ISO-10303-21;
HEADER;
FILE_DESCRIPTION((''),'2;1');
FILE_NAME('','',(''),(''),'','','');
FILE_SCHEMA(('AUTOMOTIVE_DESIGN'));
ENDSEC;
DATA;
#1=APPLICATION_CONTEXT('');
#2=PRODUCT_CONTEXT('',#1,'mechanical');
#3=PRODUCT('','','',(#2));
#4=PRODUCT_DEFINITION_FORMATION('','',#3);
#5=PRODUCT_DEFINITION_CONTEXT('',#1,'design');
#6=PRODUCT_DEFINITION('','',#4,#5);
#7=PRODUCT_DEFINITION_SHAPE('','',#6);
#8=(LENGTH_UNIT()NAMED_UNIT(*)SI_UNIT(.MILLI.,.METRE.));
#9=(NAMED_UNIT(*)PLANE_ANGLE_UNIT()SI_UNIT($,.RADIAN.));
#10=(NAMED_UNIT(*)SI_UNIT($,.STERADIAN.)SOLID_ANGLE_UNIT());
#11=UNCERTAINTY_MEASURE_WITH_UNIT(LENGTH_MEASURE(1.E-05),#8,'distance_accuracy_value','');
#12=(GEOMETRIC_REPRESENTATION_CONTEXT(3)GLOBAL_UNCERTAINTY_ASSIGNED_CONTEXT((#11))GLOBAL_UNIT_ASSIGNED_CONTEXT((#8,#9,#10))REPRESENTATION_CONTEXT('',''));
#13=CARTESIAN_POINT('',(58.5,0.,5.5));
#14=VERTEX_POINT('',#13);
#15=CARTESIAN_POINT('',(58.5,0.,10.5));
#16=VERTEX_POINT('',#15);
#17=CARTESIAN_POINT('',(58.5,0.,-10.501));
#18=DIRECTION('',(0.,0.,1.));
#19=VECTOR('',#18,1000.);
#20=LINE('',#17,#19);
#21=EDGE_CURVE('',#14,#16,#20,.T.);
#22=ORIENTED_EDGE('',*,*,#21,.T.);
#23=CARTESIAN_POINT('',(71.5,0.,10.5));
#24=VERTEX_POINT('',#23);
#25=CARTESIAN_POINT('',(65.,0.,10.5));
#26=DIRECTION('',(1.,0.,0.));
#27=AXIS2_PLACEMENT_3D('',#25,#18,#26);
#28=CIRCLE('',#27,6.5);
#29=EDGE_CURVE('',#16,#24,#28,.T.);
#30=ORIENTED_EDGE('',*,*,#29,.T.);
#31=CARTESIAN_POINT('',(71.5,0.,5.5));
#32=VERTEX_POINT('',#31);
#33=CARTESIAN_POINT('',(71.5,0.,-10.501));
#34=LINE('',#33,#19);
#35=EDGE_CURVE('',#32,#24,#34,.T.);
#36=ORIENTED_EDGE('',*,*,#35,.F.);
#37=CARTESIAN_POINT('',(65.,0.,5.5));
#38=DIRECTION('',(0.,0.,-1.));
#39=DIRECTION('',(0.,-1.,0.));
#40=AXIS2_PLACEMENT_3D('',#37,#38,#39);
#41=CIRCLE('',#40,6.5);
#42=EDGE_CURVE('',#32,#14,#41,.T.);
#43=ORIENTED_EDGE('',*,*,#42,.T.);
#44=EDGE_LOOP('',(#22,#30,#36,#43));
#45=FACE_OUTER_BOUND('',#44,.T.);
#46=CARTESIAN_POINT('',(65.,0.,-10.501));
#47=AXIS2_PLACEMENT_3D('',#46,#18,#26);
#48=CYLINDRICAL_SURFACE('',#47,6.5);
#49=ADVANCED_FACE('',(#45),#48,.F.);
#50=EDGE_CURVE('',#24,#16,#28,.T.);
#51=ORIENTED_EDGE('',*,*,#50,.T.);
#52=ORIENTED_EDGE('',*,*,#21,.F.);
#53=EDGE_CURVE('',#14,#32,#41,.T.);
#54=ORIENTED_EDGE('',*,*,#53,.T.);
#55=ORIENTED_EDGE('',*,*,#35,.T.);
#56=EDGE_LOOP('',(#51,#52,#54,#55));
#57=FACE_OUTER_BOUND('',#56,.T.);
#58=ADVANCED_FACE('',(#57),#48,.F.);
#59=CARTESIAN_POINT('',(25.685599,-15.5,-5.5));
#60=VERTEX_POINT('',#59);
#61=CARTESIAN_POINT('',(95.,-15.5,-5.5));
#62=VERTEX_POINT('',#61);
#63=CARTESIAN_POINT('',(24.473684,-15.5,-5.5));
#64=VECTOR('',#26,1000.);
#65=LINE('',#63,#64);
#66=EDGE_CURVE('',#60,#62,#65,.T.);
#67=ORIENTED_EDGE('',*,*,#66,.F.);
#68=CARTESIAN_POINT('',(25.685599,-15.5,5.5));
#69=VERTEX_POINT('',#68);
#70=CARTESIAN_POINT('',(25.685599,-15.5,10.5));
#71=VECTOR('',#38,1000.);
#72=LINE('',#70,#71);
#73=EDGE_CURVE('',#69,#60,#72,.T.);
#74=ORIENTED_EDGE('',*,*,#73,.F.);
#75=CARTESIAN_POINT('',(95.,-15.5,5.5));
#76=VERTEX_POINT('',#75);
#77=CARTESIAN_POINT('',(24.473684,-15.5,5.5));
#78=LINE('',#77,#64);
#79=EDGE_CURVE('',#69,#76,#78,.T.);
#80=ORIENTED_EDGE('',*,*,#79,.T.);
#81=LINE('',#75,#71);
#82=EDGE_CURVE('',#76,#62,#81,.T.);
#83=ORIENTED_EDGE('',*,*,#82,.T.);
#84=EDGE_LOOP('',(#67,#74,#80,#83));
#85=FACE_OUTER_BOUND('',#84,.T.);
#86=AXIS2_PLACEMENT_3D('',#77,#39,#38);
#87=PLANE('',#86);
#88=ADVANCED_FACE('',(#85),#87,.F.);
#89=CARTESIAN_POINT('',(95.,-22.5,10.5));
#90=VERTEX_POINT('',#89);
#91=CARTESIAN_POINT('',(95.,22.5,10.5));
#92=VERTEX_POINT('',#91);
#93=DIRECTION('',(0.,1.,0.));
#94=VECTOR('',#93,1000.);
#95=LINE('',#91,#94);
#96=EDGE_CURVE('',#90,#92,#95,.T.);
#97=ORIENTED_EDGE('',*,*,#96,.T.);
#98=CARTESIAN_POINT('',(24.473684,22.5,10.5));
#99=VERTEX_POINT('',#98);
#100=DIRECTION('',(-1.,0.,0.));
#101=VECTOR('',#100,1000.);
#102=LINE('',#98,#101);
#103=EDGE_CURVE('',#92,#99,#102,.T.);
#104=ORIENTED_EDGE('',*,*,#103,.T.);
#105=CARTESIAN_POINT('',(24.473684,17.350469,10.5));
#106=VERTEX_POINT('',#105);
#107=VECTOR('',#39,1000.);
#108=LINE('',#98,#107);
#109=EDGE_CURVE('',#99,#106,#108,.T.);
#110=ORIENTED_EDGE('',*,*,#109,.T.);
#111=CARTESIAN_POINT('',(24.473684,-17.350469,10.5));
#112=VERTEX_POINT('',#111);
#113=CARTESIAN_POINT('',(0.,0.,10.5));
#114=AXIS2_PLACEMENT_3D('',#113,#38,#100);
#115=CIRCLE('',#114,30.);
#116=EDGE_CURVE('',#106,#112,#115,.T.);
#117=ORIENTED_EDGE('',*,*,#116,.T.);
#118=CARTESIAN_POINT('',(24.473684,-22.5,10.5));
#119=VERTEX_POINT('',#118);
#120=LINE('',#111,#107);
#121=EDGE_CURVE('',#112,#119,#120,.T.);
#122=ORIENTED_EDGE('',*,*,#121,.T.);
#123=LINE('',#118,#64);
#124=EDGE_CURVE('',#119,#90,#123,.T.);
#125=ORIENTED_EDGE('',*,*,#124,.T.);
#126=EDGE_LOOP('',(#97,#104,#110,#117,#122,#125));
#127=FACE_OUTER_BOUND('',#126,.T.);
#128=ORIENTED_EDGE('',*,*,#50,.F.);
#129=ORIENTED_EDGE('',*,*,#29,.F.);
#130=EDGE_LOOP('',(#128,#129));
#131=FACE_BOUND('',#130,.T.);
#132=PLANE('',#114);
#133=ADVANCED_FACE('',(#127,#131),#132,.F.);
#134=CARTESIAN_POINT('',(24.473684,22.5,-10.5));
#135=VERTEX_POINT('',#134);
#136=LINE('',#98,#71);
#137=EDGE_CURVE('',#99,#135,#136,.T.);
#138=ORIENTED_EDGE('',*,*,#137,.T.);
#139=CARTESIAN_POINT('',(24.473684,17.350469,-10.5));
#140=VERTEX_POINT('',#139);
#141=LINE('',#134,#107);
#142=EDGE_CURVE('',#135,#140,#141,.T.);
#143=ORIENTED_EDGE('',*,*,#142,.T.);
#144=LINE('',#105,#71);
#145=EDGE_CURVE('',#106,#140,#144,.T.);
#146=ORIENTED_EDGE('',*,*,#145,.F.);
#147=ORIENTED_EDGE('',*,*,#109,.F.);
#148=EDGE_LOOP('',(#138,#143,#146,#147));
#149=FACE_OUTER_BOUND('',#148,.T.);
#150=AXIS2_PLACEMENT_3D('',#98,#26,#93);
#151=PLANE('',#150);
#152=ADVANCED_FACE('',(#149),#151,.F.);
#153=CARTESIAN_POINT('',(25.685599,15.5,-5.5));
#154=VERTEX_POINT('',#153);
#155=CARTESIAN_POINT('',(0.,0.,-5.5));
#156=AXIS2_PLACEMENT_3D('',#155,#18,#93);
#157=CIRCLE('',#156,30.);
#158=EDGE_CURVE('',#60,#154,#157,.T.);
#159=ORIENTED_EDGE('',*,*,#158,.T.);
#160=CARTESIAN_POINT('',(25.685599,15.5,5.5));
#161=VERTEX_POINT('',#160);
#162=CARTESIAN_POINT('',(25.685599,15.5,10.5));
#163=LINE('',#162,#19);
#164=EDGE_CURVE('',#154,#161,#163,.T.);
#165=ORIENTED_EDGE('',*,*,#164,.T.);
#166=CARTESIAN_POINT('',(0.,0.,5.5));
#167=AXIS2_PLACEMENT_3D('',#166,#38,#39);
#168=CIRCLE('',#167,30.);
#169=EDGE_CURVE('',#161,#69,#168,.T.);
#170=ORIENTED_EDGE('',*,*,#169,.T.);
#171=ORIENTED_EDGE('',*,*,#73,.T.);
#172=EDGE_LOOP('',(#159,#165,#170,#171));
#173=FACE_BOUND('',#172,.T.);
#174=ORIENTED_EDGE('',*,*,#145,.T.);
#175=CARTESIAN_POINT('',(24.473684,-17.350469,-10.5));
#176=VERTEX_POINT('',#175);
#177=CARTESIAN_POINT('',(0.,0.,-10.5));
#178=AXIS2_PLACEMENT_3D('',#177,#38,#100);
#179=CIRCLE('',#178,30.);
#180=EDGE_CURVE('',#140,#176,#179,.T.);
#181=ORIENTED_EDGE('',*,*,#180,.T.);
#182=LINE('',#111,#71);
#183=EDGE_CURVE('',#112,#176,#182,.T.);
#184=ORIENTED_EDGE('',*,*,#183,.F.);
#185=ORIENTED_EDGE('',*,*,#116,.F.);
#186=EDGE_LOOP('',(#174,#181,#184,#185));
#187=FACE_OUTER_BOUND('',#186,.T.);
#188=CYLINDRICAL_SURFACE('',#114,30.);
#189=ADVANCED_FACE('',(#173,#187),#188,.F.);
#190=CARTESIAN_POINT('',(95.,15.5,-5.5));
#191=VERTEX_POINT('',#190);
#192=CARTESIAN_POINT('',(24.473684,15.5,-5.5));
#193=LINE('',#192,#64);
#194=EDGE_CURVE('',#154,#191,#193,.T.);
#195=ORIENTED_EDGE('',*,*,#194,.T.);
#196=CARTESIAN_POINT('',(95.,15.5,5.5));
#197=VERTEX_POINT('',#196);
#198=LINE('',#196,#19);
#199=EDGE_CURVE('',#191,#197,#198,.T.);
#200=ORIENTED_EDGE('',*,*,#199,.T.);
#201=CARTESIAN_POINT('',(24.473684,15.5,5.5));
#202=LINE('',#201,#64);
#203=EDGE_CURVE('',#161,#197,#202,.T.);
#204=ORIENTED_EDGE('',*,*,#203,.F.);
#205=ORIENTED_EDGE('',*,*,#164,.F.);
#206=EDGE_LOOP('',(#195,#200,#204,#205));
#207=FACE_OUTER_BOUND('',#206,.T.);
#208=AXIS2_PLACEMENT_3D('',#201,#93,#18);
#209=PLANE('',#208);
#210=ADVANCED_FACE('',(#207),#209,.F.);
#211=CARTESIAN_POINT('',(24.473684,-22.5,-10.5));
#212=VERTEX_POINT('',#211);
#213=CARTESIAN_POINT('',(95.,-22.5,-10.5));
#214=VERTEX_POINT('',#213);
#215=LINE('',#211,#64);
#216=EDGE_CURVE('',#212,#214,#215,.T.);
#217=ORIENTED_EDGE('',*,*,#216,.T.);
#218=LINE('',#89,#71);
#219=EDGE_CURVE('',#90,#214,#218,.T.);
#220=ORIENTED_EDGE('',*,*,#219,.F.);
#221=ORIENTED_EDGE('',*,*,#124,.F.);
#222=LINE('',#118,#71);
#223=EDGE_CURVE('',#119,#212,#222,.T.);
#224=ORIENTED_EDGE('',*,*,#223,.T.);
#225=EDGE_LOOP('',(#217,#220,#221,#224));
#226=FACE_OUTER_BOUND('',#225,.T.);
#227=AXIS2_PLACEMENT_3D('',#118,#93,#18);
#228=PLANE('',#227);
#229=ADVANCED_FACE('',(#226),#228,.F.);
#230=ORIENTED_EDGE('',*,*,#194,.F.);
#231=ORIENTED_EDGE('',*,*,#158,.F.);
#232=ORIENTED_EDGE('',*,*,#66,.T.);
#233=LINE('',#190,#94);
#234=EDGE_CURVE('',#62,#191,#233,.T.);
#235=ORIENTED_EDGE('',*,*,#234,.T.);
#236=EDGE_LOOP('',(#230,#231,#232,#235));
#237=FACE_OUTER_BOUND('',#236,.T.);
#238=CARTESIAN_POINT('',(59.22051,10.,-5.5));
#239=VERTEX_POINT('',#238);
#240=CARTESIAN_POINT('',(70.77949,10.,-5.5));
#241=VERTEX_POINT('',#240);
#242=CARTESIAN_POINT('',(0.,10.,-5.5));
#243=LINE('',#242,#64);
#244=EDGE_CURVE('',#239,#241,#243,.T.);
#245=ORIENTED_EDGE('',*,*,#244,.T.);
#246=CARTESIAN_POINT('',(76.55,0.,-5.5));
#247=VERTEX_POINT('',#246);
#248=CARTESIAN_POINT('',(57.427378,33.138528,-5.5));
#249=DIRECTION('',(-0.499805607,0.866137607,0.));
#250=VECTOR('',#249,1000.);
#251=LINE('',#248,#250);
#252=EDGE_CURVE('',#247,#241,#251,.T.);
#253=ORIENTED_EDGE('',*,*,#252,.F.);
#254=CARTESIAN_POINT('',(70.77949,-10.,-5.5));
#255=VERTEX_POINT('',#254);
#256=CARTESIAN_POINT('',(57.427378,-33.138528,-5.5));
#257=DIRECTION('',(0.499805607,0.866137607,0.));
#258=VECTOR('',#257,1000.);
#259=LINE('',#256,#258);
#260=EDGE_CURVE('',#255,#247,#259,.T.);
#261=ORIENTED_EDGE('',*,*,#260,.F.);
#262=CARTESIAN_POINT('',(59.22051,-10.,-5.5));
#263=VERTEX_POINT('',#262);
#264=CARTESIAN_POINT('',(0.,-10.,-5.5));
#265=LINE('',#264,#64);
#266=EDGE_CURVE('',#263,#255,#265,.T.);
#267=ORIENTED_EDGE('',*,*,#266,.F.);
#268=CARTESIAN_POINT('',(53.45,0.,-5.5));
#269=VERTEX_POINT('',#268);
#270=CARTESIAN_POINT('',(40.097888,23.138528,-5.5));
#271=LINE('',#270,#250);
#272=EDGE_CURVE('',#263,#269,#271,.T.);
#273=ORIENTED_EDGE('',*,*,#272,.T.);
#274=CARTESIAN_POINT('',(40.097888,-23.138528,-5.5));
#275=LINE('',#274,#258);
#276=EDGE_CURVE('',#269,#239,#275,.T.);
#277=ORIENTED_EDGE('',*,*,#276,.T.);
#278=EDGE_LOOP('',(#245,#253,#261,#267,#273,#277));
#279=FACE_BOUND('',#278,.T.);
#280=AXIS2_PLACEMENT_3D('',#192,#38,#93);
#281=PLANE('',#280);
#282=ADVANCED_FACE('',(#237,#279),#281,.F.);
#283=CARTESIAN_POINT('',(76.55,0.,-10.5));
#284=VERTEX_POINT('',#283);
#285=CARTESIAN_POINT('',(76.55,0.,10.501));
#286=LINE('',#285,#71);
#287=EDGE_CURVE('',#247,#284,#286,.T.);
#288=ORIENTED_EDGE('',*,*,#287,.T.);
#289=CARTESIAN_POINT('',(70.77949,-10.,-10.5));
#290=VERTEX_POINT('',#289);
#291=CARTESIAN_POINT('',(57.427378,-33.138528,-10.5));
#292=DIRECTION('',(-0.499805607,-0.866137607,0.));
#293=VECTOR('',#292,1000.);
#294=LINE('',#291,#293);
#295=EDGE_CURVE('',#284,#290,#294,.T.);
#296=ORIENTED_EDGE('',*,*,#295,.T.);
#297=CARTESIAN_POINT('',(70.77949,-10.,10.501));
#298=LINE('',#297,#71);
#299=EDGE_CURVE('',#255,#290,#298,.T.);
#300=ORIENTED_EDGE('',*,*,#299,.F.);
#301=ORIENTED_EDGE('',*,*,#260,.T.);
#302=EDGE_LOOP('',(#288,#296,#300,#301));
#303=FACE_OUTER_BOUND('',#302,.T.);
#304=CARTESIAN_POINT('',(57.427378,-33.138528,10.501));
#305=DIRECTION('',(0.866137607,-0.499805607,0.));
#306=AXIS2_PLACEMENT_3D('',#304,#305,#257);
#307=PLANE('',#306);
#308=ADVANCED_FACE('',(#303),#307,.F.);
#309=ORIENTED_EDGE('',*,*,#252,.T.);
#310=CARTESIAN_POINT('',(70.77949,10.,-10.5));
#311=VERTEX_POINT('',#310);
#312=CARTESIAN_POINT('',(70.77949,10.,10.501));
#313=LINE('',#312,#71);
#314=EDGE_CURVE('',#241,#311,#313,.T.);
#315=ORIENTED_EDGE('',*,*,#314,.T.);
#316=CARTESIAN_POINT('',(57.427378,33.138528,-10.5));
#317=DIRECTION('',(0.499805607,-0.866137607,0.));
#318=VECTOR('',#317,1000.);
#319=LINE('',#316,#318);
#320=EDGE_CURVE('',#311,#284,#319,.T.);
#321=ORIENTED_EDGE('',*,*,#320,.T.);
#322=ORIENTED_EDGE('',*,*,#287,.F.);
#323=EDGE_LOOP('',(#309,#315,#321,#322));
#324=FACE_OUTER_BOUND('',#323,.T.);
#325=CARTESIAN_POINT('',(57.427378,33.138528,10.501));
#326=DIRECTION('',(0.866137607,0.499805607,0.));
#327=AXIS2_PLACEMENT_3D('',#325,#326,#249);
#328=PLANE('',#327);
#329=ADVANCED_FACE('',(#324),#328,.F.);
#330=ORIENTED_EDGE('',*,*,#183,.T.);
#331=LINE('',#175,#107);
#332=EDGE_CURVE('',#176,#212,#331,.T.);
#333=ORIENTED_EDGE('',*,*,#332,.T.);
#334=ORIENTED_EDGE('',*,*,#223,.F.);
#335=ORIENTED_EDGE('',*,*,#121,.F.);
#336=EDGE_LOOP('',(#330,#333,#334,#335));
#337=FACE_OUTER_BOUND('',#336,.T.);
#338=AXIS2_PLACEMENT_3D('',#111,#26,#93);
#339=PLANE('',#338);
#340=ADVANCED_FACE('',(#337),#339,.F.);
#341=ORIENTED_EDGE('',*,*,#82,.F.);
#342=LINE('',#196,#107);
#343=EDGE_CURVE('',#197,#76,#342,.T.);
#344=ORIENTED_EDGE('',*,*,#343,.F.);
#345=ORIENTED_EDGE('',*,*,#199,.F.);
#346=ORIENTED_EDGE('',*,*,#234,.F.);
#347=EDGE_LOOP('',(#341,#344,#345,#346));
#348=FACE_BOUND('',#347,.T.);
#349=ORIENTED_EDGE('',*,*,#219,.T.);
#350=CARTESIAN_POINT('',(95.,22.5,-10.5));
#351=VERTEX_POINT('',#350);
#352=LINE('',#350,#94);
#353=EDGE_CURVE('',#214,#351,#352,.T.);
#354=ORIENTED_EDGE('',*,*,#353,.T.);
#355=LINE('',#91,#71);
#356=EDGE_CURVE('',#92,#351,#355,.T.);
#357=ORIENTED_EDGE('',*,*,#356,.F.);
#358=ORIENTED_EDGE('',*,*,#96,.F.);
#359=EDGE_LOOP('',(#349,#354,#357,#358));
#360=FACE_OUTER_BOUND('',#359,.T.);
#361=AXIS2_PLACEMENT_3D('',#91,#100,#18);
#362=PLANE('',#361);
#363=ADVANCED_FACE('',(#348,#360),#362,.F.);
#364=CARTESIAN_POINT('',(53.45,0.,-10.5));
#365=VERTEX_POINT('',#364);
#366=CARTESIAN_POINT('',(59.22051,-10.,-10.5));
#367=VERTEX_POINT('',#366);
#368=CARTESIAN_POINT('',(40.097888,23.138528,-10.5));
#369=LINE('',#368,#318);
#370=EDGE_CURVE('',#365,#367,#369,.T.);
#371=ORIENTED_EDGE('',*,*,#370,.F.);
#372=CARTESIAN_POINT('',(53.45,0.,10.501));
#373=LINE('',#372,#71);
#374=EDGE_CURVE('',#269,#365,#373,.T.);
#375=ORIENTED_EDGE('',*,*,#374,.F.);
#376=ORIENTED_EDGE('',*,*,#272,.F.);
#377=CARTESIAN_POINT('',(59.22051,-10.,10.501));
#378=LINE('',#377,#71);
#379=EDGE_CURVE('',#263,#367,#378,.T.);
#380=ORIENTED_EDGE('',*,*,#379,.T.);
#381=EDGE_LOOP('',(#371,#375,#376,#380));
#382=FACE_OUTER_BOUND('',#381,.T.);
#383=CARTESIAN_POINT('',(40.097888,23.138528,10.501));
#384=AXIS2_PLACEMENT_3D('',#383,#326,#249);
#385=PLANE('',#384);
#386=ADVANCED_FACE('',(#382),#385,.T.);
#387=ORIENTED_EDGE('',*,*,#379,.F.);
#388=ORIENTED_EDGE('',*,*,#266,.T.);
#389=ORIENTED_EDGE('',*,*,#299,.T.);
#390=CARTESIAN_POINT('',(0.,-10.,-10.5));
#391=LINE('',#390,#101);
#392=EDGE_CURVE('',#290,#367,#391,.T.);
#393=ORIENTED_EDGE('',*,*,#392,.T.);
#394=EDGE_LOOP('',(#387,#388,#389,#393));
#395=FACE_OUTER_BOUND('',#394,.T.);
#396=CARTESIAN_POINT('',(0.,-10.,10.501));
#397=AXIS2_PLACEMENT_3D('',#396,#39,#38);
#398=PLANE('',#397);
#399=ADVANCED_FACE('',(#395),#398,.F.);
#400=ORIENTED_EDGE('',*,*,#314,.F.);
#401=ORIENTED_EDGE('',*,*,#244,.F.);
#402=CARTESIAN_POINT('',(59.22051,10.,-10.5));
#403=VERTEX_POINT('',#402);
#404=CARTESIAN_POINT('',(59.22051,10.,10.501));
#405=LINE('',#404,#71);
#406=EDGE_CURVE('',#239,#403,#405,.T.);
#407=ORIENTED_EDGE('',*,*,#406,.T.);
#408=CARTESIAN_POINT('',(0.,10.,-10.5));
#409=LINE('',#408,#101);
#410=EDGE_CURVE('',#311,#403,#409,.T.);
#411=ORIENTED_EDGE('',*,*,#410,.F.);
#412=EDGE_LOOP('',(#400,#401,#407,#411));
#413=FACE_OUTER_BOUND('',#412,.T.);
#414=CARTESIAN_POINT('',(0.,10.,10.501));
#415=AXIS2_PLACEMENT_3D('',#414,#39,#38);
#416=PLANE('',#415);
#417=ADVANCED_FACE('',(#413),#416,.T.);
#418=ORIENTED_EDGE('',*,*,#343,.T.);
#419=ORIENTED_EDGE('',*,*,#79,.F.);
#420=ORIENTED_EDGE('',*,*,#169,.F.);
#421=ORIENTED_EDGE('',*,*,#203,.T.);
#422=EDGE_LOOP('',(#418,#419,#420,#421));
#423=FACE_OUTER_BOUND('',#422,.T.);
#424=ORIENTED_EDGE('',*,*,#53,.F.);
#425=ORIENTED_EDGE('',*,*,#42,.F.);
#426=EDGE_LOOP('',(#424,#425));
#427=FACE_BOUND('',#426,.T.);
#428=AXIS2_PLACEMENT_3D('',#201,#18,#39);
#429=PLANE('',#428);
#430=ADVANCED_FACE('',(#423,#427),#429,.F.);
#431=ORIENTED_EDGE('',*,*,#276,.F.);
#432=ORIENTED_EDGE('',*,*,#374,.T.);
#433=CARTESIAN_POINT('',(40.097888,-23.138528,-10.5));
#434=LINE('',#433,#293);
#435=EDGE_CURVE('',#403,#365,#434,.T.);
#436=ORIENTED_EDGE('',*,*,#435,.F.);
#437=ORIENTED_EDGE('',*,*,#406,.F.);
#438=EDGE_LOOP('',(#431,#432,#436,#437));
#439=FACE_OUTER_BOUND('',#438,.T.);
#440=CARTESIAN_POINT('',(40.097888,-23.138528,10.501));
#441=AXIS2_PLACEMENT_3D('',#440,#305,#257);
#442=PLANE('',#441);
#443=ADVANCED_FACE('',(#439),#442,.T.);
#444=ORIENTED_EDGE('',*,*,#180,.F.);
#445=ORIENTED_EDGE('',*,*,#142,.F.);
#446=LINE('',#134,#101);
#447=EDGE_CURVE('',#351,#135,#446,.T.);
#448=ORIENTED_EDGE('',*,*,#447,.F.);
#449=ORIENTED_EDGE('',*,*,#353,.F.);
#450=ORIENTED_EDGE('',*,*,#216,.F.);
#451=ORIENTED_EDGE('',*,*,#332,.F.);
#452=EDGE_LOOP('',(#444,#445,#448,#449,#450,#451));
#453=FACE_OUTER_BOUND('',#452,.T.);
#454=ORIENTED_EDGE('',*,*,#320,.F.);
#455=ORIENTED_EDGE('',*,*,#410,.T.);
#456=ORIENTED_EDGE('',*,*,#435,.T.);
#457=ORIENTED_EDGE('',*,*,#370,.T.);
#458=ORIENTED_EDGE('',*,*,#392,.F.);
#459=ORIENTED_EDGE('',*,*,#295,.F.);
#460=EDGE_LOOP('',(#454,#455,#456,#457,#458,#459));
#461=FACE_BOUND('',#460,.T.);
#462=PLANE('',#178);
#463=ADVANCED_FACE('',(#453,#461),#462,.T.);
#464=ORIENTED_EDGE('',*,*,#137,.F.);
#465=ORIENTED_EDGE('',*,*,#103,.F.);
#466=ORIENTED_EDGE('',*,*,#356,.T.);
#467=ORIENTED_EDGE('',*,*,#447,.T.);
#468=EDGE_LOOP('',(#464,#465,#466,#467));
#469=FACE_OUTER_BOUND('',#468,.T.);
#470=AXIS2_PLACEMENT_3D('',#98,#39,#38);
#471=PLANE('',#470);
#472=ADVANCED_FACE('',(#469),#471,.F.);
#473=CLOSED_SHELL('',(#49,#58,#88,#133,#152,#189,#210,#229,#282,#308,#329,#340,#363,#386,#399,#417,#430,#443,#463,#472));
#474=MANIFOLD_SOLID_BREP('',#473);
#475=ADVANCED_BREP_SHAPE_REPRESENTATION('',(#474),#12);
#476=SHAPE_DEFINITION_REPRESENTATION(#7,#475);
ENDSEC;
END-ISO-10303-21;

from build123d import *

# Parameters (mm, degrees)
EXTRUDE_1_DEPTH     = 10.5
SKETCH_2_W          = 11
SKETCH_2_H          = 31
CUT_EXTRUDE_1_DEPTH = 75.76938691
CUT_EXTRUDE_2_REACH = 101.861
SKETCH_3_R          = 6.5
CUT_EXTRUDE_5_REACH = 101.861
SKETCH_4_R          = 6.5


with BuildPart() as part:
    # 草图1 → 凸台-拉伸1 (new, symmetric)
    with BuildSketch(Plane.XY):
        with BuildLine():
            Line((95, 22.5), (95, -22.5))
            Line((95, -22.5), (24.473684211, -22.5))
            Line((24.473684211, -22.5), (24.473684211, -17.350469191))
            ThreePointArc((24.473684211, -17.350469191), (30, 0), (24.473684211, 17.350469191))
            Line((24.473684211, 17.350469191), (24.473684211, 22.5))
            Line((24.473684211, 22.5), (95, 22.5))
        make_face()
    extrude(amount=EXTRUDE_1_DEPTH, both=True)

    # 草图2 → 切除-拉伸1 (cut, through all)
    with BuildSketch(Plane(origin=(95, 0, 0), x_dir=(0, 0, -1), z_dir=(1, 0, 0))):
        Rectangle(SKETCH_2_W, SKETCH_2_H)
    extrude(amount=-CUT_EXTRUDE_1_DEPTH, mode=Mode.SUBTRACT)

    # 草图3 → 切除-拉伸2 (cut, up to next)
    with BuildSketch(Plane.XY.offset(10.5), mode=Mode.PRIVATE) as cut_extrude_2_sk1:
        with Locations((65, 0)):
            Circle(SKETCH_3_R)
    cut_extrude_2_tool1 = extrude(cut_extrude_2_sk1.sketch, amount=-CUT_EXTRUDE_2_REACH, mode=Mode.PRIVATE) & part.part
    add(cut_extrude_2_tool1.solids().sort_by_distance((65, 0, 10.5))[0], mode=Mode.SUBTRACT)

    # 草图4 → 切除-拉伸5 (cut, up to next)
    with BuildSketch(Plane(origin=(0, 0, -10.5), x_dir=(-1, 0, 0), z_dir=(0, 0, -1)), mode=Mode.PRIVATE) as cut_extrude_5_sk1:
        Polygon((-76.55, 0), (-70.779489597, -10), (-59.220510403, -10), (-53.45, 0), (-59.220510403, 10), (-70.779489597, 10), align=None)
        with Locations(Location((-65, 0, 0), (0, 0, 180))):
            Circle(SKETCH_4_R, mode=Mode.SUBTRACT)
    cut_extrude_5_tool1 = extrude(cut_extrude_5_sk1.sketch, amount=-CUT_EXTRUDE_5_REACH, mode=Mode.PRIVATE) & part.part
    # 草图4 → 切除-拉伸5 (cut, up to next)
    with BuildSketch(Plane(origin=(0, 0, -10.5), x_dir=(-1, 0, 0), z_dir=(0, 0, -1)), mode=Mode.PRIVATE) as cut_extrude_5_sk2:
        with Locations(Location((-65, 0, 0), (0, 0, 180))):
            Circle(SKETCH_4_R)
    cut_extrude_5_tool2 = extrude(cut_extrude_5_sk2.sketch, amount=-CUT_EXTRUDE_5_REACH, mode=Mode.PRIVATE) & part.part
    add(cut_extrude_5_tool1.solids().sort_by_distance((73.400096, -4.847284, -10.5))[0], mode=Mode.SUBTRACT)
    add(cut_extrude_5_tool2.solids().sort_by_distance((65, 0, -10.5))[0], mode=Mode.SUBTRACT)


solid = part.part
